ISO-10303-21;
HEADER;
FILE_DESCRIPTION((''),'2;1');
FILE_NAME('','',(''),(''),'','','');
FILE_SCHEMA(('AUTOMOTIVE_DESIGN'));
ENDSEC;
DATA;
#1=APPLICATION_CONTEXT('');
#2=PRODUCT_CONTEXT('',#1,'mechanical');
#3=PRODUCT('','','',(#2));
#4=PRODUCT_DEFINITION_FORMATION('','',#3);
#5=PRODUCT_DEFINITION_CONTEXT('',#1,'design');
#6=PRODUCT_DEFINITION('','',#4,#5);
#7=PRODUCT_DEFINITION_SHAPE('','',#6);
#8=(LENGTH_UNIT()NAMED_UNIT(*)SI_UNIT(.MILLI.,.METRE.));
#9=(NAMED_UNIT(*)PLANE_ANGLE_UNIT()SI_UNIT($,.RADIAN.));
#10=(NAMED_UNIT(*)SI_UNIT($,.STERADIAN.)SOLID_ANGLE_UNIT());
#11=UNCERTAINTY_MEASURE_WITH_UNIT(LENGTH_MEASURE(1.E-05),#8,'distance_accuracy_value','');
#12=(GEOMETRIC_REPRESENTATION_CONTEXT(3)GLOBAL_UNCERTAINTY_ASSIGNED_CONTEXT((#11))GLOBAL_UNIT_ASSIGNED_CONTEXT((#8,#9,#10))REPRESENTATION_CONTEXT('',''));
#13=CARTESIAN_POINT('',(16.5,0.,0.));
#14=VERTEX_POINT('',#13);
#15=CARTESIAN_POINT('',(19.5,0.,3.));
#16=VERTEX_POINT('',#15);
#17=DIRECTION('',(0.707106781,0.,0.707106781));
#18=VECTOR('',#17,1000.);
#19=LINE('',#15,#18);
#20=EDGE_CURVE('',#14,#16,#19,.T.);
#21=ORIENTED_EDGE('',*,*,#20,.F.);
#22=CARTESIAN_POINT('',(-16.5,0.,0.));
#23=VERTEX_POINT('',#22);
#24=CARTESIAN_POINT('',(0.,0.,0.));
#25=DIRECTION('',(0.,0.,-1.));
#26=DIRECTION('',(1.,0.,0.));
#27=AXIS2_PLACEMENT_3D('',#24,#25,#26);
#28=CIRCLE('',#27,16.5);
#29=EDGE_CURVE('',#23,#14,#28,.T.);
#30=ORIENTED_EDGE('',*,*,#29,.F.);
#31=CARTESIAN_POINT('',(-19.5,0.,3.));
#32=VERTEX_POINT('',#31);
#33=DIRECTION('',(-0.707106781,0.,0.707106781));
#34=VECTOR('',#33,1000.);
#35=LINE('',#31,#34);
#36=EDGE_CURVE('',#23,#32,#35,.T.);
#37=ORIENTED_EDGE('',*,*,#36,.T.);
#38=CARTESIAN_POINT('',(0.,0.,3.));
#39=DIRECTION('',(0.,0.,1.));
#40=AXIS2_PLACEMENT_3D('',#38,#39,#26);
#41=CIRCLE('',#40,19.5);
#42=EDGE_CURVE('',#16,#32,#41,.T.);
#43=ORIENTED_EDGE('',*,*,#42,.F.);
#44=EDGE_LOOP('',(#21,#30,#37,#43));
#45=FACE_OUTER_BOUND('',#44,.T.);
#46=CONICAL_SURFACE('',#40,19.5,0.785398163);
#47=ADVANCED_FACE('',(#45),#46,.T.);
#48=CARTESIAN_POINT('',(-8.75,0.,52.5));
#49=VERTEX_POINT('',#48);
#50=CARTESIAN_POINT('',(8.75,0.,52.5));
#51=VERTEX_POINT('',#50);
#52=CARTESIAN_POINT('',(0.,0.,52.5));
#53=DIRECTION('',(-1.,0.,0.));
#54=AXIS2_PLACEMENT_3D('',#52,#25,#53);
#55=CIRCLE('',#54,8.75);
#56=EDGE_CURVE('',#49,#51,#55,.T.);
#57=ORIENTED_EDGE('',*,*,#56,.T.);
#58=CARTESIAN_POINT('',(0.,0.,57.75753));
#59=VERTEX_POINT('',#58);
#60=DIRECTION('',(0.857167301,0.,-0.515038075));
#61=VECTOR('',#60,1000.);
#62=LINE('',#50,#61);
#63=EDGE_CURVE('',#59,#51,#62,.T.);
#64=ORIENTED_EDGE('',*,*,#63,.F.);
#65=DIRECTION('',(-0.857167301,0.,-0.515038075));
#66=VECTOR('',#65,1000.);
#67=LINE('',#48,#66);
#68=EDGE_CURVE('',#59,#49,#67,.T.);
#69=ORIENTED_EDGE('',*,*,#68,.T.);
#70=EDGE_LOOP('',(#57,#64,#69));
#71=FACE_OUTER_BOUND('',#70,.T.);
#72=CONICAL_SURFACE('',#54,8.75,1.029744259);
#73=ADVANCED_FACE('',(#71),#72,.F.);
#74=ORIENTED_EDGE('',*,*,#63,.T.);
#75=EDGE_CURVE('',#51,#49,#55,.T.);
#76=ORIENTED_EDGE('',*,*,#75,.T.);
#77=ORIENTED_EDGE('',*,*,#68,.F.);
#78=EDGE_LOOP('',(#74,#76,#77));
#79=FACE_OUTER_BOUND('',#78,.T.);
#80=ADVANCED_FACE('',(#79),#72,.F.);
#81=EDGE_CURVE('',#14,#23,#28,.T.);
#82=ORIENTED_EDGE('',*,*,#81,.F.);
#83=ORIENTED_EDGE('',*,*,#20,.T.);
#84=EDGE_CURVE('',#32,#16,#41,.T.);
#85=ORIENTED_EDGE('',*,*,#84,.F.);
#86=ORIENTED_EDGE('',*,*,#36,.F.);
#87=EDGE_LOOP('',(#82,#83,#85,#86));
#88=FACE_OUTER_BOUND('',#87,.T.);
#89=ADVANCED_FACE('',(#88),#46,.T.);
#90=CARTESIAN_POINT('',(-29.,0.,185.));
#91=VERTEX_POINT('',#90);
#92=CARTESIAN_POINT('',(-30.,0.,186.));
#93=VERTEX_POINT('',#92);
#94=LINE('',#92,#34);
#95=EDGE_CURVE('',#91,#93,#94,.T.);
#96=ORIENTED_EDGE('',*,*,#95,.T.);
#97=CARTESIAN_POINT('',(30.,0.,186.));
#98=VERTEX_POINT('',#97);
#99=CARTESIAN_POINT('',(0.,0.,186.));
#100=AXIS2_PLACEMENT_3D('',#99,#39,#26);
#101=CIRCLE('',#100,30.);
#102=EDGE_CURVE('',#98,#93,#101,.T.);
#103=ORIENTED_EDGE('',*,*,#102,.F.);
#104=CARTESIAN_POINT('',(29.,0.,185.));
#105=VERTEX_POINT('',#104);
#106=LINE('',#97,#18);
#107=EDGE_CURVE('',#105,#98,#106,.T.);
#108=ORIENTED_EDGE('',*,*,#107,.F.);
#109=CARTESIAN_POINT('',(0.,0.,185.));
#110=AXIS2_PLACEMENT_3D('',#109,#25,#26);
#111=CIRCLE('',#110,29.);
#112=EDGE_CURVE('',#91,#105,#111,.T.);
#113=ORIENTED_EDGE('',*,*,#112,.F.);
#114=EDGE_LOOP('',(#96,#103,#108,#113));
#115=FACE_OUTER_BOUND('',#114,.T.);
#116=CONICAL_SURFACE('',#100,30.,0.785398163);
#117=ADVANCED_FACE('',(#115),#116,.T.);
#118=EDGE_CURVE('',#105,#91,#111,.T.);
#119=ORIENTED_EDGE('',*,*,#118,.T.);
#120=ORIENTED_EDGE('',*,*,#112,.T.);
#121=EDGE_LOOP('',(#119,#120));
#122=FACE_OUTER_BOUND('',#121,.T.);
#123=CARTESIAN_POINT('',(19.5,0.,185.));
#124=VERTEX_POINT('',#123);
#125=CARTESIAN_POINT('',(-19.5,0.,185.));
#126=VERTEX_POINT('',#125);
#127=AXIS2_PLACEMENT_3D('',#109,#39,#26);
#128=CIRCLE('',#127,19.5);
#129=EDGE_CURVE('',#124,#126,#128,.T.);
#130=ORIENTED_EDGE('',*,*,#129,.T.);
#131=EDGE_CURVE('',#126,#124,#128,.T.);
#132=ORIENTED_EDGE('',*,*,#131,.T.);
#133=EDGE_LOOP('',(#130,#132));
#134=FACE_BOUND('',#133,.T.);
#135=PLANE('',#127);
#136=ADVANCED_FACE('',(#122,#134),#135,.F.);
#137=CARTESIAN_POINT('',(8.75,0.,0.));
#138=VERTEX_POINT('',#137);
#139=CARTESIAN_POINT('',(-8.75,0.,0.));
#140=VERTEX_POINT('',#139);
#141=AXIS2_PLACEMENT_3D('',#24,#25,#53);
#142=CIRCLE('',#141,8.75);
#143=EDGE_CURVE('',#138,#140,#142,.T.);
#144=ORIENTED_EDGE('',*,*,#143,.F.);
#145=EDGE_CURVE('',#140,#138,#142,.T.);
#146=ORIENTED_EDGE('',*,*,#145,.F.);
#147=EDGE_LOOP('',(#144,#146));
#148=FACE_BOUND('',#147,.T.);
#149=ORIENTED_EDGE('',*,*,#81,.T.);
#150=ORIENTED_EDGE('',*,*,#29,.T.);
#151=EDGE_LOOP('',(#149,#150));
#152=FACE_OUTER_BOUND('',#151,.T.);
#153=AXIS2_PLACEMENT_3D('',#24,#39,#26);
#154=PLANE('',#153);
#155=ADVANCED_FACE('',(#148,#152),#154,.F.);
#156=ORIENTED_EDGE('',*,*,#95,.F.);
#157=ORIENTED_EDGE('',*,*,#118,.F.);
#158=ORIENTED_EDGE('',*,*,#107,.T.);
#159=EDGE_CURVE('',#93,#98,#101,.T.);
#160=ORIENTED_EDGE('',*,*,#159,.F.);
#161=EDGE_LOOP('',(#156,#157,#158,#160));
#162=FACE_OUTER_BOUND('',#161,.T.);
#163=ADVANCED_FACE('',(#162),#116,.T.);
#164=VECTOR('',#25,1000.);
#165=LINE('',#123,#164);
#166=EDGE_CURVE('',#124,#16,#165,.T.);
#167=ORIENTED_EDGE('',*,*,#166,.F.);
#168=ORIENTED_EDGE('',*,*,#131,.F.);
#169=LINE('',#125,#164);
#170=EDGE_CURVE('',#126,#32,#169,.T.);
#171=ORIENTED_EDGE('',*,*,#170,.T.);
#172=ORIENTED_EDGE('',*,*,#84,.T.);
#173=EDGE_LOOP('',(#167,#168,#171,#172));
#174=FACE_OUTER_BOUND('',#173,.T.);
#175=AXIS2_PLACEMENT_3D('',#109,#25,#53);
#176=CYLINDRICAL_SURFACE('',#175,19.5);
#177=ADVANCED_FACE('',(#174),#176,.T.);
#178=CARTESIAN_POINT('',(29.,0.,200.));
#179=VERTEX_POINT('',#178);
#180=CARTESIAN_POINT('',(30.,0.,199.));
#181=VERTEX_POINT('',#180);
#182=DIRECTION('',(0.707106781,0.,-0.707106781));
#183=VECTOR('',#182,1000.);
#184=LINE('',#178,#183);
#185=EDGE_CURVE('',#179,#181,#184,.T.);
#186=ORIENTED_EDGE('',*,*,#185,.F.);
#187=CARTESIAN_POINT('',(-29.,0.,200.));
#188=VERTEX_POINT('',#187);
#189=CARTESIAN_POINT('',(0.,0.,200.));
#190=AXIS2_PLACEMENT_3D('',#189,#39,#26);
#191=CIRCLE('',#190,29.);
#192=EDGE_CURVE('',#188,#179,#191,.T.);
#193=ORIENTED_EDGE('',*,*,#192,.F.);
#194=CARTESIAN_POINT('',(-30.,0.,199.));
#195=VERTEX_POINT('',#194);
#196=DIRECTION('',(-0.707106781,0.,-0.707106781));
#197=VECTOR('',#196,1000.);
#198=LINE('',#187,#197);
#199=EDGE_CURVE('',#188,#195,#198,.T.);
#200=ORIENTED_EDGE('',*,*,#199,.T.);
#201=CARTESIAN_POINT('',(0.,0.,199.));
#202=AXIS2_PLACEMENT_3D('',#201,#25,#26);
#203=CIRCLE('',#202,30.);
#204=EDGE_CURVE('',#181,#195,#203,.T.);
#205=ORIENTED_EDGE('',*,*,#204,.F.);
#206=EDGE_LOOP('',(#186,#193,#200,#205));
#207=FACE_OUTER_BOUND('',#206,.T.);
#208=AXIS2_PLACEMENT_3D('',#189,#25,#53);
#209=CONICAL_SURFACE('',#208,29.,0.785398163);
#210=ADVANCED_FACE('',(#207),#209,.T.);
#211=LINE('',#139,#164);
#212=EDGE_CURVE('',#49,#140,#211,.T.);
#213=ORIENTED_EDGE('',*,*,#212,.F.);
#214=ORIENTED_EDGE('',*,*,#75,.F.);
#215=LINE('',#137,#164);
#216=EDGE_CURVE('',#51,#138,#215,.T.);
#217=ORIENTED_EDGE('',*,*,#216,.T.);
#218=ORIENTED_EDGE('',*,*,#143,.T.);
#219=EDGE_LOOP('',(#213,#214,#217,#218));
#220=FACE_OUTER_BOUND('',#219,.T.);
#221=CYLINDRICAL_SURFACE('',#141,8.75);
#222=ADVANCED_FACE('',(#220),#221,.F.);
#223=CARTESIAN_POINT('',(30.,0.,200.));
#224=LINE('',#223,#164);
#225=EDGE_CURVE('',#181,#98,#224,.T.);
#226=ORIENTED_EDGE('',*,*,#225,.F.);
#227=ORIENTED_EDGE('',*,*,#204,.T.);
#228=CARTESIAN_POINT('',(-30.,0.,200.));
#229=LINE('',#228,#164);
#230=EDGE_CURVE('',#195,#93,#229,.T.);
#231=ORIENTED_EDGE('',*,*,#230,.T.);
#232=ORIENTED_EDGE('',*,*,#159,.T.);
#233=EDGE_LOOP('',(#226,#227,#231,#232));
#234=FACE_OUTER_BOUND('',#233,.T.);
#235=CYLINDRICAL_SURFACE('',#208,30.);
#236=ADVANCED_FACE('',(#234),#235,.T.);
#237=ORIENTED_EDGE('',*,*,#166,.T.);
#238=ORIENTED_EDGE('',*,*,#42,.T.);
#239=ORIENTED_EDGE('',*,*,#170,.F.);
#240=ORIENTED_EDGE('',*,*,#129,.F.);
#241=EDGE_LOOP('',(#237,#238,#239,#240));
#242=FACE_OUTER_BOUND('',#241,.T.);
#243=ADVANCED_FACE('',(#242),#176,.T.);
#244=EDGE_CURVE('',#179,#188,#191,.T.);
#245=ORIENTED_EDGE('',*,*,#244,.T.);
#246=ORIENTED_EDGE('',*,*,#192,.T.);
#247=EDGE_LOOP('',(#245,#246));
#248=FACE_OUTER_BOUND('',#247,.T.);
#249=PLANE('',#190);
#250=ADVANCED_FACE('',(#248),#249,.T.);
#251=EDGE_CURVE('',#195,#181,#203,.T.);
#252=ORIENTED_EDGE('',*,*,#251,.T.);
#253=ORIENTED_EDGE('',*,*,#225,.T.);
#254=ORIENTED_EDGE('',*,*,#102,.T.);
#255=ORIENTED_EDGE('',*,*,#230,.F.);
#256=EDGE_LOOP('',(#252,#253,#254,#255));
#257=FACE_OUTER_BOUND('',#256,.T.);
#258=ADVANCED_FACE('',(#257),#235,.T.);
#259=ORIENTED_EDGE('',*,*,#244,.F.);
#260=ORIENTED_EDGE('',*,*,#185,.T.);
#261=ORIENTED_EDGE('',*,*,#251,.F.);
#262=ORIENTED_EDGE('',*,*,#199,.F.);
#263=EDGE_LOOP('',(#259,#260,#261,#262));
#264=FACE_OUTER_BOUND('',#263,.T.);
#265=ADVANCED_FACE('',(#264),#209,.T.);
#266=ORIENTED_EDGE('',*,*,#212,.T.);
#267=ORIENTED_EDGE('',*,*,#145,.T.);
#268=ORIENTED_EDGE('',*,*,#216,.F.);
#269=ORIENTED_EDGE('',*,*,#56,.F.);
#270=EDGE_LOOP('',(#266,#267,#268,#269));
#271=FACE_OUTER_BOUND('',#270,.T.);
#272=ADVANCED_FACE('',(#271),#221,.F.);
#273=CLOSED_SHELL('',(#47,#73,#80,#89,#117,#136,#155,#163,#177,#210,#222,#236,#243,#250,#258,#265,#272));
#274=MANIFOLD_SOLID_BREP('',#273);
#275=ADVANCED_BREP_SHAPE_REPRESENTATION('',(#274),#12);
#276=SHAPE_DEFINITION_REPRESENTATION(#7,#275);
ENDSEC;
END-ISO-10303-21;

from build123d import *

# Parameters (mm, degrees)
SKETCH1_R              = 19.5
BOSS_EXTRUDE1_DEPTH    = 185
SKETCH2_R              = 30
BOSS_EXTRUDE2_DEPTH    = 15
CHAMFER1_SIZE          = 3
CHAMFER2_SIZE          = 1
M20_TAPPED_HOLE1_D     = 17.5
M20_TAPPED_HOLE1_DEPTH = 52.5
M20_TAPPED_HOLE1_TIP   = 5.257530416


with BuildPart() as part:
    # Sketch1 → Boss-Extrude1 (new body)
    with BuildSketch(Plane.XY):
        Circle(SKETCH1_R)
    extrude(amount=BOSS_EXTRUDE1_DEPTH)

    # Sketch2 → Boss-Extrude2 (add)
    with BuildSketch(Plane.XY.offset(185)):
        Circle(SKETCH2_R)
    extrude(amount=BOSS_EXTRUDE2_DEPTH)

    # Chamfer1
    chamfer1_edges = [part.edges().sort_by_distance(p)[0] for p in [
        (-19.5, 0, 0),
    ]]
    chamfer(chamfer1_edges, length=CHAMFER1_SIZE)

    # Chamfer2
    chamfer2_edges = [part.edges().sort_by_distance(p)[0] for p in [
        (-30, 0, 185),
        (-30, 0, 200),
    ]]
    chamfer(chamfer2_edges, length=CHAMFER2_SIZE)

    # M20 Tapped Hole1
    with Locations(Plane(origin=(0, 0, 0), x_dir=(-1, 0, 0), z_dir=(0, 0, -1))):
        with Locations((0, 0)):
            Hole(M20_TAPPED_HOLE1_D / 2, depth=M20_TAPPED_HOLE1_DEPTH)
            with Locations((0, 0, -(M20_TAPPED_HOLE1_DEPTH + M20_TAPPED_HOLE1_TIP / 2))):  # 118° drill point
                Cone(0, M20_TAPPED_HOLE1_D / 2, M20_TAPPED_HOLE1_TIP, mode=Mode.SUBTRACT)


solid = part.part
